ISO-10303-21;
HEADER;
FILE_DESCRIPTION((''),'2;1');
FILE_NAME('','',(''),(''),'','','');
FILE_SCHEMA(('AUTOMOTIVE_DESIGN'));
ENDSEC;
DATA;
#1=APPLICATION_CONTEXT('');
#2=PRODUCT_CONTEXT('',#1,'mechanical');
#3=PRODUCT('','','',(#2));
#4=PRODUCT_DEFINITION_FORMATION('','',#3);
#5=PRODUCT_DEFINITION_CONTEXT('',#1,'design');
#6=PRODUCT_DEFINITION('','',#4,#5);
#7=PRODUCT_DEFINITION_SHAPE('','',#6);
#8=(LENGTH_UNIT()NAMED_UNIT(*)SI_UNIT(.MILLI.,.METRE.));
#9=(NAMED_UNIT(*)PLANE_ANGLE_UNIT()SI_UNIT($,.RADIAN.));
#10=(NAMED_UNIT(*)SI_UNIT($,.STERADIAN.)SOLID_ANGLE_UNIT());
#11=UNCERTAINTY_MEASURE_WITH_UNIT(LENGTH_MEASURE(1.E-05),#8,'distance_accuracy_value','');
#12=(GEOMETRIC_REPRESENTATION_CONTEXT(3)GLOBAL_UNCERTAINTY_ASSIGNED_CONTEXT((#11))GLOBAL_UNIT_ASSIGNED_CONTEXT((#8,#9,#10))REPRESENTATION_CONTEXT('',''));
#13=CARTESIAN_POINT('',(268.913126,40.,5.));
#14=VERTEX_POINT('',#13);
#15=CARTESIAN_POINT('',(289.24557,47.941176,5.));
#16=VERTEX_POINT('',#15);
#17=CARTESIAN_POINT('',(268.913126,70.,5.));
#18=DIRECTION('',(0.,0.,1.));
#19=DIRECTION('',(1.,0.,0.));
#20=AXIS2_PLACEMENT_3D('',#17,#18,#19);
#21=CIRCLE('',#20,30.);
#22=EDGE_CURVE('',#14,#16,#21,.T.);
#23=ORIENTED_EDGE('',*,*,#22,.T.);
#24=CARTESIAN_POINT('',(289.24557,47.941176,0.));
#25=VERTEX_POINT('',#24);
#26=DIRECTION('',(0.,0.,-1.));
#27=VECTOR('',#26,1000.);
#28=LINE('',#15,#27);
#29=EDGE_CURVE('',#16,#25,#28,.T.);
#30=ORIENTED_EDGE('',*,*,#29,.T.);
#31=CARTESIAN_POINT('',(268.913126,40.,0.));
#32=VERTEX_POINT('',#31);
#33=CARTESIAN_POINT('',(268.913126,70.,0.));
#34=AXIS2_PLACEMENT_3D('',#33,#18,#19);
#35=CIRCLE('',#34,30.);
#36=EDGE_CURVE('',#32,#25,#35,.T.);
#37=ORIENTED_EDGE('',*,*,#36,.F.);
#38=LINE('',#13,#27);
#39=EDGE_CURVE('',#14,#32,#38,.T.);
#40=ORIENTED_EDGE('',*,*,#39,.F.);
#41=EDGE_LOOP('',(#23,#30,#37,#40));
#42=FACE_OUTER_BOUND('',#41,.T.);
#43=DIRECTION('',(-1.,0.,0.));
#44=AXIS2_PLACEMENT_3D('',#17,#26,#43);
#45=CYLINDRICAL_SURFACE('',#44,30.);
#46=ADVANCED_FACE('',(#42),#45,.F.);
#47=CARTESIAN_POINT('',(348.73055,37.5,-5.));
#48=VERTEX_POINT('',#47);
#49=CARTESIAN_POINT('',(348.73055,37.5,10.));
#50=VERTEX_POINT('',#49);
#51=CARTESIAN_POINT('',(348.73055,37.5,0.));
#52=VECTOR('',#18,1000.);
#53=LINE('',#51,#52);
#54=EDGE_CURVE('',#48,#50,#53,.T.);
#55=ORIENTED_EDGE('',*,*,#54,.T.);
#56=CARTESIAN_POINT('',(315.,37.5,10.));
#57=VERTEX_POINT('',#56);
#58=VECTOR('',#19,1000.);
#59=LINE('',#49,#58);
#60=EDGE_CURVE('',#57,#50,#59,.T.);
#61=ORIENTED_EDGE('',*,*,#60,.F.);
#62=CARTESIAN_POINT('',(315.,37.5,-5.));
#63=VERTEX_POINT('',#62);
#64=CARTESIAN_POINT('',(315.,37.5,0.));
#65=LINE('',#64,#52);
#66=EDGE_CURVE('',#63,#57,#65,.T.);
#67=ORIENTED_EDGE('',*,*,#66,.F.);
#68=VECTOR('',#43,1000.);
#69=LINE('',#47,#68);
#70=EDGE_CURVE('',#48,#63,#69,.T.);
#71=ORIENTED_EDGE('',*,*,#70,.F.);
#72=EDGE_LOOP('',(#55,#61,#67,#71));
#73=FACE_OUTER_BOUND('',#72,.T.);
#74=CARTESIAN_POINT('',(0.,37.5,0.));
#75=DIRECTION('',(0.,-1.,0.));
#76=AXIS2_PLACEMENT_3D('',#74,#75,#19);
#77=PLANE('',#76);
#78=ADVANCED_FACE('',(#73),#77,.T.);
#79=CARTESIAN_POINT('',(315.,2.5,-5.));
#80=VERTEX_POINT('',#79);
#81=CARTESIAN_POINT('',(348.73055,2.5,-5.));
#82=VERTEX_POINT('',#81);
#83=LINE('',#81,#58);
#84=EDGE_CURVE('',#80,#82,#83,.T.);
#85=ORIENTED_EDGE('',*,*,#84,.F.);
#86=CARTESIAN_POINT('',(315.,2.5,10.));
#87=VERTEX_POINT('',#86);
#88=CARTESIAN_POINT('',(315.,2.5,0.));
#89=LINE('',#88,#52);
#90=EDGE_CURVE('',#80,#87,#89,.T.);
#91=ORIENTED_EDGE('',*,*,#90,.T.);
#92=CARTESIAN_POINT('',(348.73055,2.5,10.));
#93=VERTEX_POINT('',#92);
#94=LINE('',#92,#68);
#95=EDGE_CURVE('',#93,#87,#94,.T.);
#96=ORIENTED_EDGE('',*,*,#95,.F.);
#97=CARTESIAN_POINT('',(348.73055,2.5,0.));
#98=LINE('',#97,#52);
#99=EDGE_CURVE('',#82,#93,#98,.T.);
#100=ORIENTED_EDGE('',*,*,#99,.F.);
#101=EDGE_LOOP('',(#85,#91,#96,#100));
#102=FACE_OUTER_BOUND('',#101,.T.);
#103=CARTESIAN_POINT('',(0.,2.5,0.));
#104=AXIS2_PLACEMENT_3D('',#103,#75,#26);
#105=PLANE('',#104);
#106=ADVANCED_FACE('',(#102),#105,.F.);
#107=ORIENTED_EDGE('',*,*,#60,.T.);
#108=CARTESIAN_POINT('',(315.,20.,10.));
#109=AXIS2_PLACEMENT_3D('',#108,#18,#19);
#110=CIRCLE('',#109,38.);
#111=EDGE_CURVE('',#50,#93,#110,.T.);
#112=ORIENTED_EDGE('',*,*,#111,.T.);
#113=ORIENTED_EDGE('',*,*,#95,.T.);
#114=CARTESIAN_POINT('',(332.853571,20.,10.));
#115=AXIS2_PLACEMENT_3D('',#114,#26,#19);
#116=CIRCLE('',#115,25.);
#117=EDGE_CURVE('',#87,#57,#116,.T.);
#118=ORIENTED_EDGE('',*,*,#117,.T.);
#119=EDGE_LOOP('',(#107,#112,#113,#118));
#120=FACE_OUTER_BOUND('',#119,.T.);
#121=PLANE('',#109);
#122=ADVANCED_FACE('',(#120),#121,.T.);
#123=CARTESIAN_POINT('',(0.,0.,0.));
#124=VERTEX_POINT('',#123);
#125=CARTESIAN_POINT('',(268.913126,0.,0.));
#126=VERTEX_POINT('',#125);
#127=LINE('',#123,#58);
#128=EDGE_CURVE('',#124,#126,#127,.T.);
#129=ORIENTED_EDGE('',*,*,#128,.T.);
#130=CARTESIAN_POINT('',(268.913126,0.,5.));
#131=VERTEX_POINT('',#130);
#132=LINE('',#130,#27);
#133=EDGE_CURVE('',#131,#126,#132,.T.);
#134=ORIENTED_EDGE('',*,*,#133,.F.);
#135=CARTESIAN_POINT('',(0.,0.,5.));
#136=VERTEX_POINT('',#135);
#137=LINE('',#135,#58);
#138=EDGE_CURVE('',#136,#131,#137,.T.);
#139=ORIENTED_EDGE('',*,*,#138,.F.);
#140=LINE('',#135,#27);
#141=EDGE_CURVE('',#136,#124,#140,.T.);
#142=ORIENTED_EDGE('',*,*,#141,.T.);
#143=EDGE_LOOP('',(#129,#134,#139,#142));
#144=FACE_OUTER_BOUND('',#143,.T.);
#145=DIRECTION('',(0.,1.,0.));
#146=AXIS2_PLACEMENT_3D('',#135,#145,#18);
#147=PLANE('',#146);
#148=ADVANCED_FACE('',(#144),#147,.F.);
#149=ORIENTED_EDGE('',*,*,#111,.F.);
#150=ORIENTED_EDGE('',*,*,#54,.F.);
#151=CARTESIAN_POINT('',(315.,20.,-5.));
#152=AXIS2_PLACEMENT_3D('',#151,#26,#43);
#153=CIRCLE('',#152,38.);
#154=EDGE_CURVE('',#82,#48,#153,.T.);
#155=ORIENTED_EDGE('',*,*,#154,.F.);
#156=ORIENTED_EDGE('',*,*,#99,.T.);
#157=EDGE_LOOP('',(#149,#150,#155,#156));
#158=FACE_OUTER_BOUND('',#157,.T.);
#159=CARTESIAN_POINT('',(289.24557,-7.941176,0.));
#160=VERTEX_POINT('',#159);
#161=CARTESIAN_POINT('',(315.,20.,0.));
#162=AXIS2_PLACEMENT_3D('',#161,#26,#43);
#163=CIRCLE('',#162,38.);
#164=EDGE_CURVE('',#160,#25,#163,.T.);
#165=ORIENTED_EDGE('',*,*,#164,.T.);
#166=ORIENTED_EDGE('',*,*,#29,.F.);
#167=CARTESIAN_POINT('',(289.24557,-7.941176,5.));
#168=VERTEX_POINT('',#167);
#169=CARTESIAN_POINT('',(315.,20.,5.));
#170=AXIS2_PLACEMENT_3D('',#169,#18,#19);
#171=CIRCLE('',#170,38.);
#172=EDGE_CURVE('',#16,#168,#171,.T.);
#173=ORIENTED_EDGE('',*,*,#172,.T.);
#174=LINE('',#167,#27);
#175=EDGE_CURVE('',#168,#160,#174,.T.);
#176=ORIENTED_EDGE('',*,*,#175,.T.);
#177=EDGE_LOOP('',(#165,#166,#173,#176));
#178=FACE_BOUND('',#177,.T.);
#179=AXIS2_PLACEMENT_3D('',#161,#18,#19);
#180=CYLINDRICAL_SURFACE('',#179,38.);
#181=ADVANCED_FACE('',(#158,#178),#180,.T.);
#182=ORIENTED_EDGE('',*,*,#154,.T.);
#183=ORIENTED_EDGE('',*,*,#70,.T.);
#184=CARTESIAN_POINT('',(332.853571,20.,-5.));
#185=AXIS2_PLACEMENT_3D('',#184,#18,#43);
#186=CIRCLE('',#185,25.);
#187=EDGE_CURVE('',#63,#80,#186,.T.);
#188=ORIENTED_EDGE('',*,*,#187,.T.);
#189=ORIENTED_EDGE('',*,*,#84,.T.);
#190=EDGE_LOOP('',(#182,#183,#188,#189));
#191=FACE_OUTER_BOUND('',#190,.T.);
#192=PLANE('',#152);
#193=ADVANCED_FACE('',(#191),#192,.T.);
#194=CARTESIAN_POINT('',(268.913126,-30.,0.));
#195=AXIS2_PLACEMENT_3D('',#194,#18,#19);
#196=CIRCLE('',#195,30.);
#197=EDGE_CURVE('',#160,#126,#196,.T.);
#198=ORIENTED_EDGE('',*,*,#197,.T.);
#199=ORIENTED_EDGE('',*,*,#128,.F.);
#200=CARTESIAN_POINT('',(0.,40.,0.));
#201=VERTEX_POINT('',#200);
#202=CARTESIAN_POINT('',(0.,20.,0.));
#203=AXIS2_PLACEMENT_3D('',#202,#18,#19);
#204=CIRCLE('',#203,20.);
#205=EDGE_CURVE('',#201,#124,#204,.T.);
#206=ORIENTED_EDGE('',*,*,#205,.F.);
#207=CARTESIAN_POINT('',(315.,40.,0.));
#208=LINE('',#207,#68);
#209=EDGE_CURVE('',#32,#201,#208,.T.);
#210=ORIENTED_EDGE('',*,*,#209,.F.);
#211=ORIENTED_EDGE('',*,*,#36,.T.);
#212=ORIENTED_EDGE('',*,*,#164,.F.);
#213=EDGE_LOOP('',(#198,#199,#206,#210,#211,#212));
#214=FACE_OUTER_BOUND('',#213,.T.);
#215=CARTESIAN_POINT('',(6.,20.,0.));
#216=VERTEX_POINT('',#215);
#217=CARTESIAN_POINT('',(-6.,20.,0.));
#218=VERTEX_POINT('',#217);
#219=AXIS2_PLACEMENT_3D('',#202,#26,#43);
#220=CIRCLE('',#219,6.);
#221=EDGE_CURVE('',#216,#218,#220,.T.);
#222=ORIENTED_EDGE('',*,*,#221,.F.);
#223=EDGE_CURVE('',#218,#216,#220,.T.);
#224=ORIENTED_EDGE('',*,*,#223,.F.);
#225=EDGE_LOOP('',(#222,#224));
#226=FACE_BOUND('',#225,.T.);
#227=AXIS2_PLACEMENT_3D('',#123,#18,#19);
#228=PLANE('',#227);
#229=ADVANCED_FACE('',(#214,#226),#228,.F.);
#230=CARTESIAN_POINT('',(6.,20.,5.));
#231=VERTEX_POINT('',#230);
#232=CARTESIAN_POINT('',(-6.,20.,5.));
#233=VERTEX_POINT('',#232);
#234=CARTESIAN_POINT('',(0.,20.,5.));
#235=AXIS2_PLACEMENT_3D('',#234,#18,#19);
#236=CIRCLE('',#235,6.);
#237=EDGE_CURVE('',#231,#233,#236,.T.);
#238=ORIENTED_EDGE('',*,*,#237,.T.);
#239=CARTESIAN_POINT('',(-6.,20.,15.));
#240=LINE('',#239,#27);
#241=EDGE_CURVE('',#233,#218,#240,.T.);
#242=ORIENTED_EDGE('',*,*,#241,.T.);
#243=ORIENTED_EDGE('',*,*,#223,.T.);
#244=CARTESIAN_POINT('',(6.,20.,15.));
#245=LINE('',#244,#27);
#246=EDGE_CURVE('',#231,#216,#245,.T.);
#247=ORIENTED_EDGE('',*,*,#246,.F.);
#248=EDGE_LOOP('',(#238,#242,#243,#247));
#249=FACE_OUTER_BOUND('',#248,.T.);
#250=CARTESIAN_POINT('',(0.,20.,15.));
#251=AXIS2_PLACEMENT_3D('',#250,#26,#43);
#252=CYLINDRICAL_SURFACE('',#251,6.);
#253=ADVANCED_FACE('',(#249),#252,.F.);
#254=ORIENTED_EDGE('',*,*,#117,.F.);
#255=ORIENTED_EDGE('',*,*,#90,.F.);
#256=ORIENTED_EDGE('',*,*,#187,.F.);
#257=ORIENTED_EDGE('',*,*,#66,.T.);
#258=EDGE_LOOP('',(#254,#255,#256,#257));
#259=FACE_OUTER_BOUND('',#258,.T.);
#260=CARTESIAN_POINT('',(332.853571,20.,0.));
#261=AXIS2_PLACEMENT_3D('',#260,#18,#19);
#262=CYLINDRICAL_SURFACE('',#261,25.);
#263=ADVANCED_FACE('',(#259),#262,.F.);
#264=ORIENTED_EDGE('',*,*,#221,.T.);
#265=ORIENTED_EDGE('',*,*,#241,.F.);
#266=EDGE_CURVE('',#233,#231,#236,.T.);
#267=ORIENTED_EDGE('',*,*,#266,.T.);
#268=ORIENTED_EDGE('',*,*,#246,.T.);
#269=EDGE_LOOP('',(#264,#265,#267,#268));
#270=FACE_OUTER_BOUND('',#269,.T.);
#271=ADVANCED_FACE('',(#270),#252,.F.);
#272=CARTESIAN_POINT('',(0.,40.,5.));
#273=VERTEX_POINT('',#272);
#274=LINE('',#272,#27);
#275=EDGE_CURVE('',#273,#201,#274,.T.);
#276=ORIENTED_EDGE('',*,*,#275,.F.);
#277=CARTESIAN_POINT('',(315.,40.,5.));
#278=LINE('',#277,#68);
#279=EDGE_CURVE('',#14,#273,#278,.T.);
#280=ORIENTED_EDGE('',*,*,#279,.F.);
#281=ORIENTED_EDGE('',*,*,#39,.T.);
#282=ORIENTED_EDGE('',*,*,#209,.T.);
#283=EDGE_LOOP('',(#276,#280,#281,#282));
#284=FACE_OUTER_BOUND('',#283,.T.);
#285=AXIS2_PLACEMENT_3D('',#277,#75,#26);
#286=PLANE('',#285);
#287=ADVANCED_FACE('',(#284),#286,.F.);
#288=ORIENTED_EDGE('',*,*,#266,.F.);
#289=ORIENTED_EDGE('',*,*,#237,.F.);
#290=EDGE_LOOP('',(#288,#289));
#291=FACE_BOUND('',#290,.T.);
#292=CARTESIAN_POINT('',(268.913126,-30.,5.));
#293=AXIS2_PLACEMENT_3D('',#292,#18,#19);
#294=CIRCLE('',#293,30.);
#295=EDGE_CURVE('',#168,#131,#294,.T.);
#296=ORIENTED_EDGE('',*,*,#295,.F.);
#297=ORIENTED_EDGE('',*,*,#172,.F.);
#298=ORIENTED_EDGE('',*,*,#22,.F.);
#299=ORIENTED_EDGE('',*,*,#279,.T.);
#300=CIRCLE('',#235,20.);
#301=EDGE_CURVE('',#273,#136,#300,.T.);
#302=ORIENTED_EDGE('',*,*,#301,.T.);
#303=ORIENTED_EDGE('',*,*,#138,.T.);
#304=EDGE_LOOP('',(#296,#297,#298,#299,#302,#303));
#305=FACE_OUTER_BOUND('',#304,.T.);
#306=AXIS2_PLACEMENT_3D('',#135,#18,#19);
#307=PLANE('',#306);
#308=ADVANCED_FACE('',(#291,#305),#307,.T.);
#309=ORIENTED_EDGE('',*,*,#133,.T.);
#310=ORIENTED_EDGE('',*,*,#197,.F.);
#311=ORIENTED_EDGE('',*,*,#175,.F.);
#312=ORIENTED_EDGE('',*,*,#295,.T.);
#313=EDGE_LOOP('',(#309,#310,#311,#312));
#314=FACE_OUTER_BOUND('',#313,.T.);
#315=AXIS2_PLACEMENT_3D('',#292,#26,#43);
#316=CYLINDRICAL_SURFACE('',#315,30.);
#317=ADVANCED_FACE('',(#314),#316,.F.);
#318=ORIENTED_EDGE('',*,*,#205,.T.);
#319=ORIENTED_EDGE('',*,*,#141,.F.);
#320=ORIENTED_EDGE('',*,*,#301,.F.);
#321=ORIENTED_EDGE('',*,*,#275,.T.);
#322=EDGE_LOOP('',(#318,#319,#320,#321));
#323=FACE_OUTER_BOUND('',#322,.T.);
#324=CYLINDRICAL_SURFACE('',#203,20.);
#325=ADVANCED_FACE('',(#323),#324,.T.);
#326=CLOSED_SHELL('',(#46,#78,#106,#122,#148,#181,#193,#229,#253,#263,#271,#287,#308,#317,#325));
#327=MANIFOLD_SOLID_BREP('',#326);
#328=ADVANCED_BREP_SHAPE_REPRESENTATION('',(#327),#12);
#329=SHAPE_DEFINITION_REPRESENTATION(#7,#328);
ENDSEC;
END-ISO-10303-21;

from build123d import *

# Parameters (mm, degrees)
HANDLE_PROFILE_SKETCH_W   = 315
HANDLE_PROFILE_SKETCH_H   = 40
HANDLE_BAR_315X40X5_DEPTH = 5
HANGING_END_SKETCH_R      = 20
ROUNDED_HANGING_END_DEPTH = 5
HEAD_NECK_BOSS_DEPTH      = 5
NECK_TRIM_CUT_R25_DEPTH   = 5
NECK_START                = 5
NECK_FILL_BOSS_A_DEPTH    = 5
NECK_FILL_BOSS_B_DEPTH    = 5
OPEN_START                = -5
OPEN_JAW_HEAD_DEPTH       = 5
HANGING_HOLE_SKETCH_R     = 6
HANGING_HOLE_6_DEPTH      = 15


with BuildPart() as part:
    # Handle Profile Sketch → Handle Bar 315x40x5 (new body)
    with BuildSketch(Plane.XY):
        with Locations((157.5, 20)):
            Rectangle(HANDLE_PROFILE_SKETCH_W, HANDLE_PROFILE_SKETCH_H)
    extrude(amount=HANDLE_BAR_315X40X5_DEPTH)

    # Hanging End Sketch → Rounded Hanging End (add)
    with BuildSketch(Plane.XY.offset(5)):
        with Locations((0, 20)):
            Circle(HANGING_END_SKETCH_R)
    extrude(amount=-ROUNDED_HANGING_END_DEPTH)

    # Neck Profile Sketch → Head Neck Boss (add)
    with BuildSketch(Plane.XY.offset(5)):
        with BuildLine():
            Line((315, 40), (315, 37.5))
            Line((315, 37.5), (348.730549951, 37.5))
            ThreePointArc((348.730549951, 37.5), (316.43745902, 57.972802261), (282.689011157, 40))
            Line((282.689011157, 40), (315, 40))
        make_face()
        with BuildLine():
            Line((348.730549951, 2.5), (315, 2.5))
            Line((315, 2.5), (315, 0))
            Line((315, 0), (282.689011157, 0))
            ThreePointArc((282.689011157, 0), (316.43745902, -17.972802261), (348.730549951, 2.5))
        make_face()
    extrude(amount=-HEAD_NECK_BOSS_DEPTH)

    # Neck Trim Sketch R25 → Neck Trim Cut R25 (cut)
    with BuildSketch(Plane.XY.offset(5)):
        with BuildLine():
            Line((315, 37.5), (315, 2.5))
            ThreePointArc((315, 2.5), (307.853571071, 20), (315, 37.5))
        make_face()
    extrude(amount=-NECK_TRIM_CUT_R25_DEPTH, mode=Mode.SUBTRACT)

    # Neck Fill Sketch A → Neck Fill Boss A (add)
    with BuildSketch(Plane.XY.offset(5).offset(NECK_START)):
        with BuildLine():
            Line((348.730549951, 37.5), (315, 37.5))
            ThreePointArc((315, 37.5), (307.853571071, 20), (315, 2.5))
            Line((315, 2.5), (348.730549951, 2.5))
            ThreePointArc((348.730549951, 2.5), (277, 20), (348.730549951, 37.5))
        make_face()
    extrude(amount=-NECK_FILL_BOSS_A_DEPTH)

    # Neck Fill Sketch B → Neck Fill Boss B (add)
    with BuildSketch(Plane(origin=(0, 0, 0), x_dir=(-1, 0, 0), z_dir=(0, 0, -1))):
        with BuildLine():
            Line((-348.730549951, 37.5), (-315, 37.5))
            ThreePointArc((-315, 37.5), (-307.853571071, 20), (-315, 2.5))
            Line((-315, 2.5), (-348.730549951, 2.5))
            ThreePointArc((-348.730549951, 2.5), (-277, 20), (-348.730549951, 37.5))
        make_face()
    extrude(amount=NECK_FILL_BOSS_B_DEPTH)

    # Jaw Head Sketch → Open Jaw Head (add)
    with BuildSketch(Plane(origin=(0, 0, 0), x_dir=(-1, 0, 0), z_dir=(0, 0, -1)).offset(OPEN_START)):
        with BuildLine():
            Line((-268.913125513, 40), (-282.689011157, 40))
            ThreePointArc((-282.689011157, 40), (-285.697034566, 44.193722673), (-289.245570139, 47.941176471))
            ThreePointArc((-289.245570139, 47.941176471), (-279.827228639, 42.055727726), (-268.913125513, 40))
        make_face()
        with BuildLine():
            Line((-268.913125513, 0), (-282.689011157, 0))
            ThreePointArc((-282.689011157, 0), (-285.697034566, -4.193722673), (-289.245570139, -7.941176471))
            ThreePointArc((-289.245570139, -7.941176471), (-279.827228639, -2.055727726), (-268.913125513, 0))
        make_face()
    extrude(amount=OPEN_JAW_HEAD_DEPTH)

    # Hanging Hole Sketch → Hanging Hole Ø6 (cut)
    with BuildSketch(Plane(origin=(0, 0, 0), x_dir=(-1, 0, 0), z_dir=(0, 0, -1))):
        with Locations((0, 20)):
            Circle(HANGING_HOLE_SKETCH_R)
    extrude(amount=-HANGING_HOLE_6_DEPTH, mode=Mode.SUBTRACT)


solid = part.part
